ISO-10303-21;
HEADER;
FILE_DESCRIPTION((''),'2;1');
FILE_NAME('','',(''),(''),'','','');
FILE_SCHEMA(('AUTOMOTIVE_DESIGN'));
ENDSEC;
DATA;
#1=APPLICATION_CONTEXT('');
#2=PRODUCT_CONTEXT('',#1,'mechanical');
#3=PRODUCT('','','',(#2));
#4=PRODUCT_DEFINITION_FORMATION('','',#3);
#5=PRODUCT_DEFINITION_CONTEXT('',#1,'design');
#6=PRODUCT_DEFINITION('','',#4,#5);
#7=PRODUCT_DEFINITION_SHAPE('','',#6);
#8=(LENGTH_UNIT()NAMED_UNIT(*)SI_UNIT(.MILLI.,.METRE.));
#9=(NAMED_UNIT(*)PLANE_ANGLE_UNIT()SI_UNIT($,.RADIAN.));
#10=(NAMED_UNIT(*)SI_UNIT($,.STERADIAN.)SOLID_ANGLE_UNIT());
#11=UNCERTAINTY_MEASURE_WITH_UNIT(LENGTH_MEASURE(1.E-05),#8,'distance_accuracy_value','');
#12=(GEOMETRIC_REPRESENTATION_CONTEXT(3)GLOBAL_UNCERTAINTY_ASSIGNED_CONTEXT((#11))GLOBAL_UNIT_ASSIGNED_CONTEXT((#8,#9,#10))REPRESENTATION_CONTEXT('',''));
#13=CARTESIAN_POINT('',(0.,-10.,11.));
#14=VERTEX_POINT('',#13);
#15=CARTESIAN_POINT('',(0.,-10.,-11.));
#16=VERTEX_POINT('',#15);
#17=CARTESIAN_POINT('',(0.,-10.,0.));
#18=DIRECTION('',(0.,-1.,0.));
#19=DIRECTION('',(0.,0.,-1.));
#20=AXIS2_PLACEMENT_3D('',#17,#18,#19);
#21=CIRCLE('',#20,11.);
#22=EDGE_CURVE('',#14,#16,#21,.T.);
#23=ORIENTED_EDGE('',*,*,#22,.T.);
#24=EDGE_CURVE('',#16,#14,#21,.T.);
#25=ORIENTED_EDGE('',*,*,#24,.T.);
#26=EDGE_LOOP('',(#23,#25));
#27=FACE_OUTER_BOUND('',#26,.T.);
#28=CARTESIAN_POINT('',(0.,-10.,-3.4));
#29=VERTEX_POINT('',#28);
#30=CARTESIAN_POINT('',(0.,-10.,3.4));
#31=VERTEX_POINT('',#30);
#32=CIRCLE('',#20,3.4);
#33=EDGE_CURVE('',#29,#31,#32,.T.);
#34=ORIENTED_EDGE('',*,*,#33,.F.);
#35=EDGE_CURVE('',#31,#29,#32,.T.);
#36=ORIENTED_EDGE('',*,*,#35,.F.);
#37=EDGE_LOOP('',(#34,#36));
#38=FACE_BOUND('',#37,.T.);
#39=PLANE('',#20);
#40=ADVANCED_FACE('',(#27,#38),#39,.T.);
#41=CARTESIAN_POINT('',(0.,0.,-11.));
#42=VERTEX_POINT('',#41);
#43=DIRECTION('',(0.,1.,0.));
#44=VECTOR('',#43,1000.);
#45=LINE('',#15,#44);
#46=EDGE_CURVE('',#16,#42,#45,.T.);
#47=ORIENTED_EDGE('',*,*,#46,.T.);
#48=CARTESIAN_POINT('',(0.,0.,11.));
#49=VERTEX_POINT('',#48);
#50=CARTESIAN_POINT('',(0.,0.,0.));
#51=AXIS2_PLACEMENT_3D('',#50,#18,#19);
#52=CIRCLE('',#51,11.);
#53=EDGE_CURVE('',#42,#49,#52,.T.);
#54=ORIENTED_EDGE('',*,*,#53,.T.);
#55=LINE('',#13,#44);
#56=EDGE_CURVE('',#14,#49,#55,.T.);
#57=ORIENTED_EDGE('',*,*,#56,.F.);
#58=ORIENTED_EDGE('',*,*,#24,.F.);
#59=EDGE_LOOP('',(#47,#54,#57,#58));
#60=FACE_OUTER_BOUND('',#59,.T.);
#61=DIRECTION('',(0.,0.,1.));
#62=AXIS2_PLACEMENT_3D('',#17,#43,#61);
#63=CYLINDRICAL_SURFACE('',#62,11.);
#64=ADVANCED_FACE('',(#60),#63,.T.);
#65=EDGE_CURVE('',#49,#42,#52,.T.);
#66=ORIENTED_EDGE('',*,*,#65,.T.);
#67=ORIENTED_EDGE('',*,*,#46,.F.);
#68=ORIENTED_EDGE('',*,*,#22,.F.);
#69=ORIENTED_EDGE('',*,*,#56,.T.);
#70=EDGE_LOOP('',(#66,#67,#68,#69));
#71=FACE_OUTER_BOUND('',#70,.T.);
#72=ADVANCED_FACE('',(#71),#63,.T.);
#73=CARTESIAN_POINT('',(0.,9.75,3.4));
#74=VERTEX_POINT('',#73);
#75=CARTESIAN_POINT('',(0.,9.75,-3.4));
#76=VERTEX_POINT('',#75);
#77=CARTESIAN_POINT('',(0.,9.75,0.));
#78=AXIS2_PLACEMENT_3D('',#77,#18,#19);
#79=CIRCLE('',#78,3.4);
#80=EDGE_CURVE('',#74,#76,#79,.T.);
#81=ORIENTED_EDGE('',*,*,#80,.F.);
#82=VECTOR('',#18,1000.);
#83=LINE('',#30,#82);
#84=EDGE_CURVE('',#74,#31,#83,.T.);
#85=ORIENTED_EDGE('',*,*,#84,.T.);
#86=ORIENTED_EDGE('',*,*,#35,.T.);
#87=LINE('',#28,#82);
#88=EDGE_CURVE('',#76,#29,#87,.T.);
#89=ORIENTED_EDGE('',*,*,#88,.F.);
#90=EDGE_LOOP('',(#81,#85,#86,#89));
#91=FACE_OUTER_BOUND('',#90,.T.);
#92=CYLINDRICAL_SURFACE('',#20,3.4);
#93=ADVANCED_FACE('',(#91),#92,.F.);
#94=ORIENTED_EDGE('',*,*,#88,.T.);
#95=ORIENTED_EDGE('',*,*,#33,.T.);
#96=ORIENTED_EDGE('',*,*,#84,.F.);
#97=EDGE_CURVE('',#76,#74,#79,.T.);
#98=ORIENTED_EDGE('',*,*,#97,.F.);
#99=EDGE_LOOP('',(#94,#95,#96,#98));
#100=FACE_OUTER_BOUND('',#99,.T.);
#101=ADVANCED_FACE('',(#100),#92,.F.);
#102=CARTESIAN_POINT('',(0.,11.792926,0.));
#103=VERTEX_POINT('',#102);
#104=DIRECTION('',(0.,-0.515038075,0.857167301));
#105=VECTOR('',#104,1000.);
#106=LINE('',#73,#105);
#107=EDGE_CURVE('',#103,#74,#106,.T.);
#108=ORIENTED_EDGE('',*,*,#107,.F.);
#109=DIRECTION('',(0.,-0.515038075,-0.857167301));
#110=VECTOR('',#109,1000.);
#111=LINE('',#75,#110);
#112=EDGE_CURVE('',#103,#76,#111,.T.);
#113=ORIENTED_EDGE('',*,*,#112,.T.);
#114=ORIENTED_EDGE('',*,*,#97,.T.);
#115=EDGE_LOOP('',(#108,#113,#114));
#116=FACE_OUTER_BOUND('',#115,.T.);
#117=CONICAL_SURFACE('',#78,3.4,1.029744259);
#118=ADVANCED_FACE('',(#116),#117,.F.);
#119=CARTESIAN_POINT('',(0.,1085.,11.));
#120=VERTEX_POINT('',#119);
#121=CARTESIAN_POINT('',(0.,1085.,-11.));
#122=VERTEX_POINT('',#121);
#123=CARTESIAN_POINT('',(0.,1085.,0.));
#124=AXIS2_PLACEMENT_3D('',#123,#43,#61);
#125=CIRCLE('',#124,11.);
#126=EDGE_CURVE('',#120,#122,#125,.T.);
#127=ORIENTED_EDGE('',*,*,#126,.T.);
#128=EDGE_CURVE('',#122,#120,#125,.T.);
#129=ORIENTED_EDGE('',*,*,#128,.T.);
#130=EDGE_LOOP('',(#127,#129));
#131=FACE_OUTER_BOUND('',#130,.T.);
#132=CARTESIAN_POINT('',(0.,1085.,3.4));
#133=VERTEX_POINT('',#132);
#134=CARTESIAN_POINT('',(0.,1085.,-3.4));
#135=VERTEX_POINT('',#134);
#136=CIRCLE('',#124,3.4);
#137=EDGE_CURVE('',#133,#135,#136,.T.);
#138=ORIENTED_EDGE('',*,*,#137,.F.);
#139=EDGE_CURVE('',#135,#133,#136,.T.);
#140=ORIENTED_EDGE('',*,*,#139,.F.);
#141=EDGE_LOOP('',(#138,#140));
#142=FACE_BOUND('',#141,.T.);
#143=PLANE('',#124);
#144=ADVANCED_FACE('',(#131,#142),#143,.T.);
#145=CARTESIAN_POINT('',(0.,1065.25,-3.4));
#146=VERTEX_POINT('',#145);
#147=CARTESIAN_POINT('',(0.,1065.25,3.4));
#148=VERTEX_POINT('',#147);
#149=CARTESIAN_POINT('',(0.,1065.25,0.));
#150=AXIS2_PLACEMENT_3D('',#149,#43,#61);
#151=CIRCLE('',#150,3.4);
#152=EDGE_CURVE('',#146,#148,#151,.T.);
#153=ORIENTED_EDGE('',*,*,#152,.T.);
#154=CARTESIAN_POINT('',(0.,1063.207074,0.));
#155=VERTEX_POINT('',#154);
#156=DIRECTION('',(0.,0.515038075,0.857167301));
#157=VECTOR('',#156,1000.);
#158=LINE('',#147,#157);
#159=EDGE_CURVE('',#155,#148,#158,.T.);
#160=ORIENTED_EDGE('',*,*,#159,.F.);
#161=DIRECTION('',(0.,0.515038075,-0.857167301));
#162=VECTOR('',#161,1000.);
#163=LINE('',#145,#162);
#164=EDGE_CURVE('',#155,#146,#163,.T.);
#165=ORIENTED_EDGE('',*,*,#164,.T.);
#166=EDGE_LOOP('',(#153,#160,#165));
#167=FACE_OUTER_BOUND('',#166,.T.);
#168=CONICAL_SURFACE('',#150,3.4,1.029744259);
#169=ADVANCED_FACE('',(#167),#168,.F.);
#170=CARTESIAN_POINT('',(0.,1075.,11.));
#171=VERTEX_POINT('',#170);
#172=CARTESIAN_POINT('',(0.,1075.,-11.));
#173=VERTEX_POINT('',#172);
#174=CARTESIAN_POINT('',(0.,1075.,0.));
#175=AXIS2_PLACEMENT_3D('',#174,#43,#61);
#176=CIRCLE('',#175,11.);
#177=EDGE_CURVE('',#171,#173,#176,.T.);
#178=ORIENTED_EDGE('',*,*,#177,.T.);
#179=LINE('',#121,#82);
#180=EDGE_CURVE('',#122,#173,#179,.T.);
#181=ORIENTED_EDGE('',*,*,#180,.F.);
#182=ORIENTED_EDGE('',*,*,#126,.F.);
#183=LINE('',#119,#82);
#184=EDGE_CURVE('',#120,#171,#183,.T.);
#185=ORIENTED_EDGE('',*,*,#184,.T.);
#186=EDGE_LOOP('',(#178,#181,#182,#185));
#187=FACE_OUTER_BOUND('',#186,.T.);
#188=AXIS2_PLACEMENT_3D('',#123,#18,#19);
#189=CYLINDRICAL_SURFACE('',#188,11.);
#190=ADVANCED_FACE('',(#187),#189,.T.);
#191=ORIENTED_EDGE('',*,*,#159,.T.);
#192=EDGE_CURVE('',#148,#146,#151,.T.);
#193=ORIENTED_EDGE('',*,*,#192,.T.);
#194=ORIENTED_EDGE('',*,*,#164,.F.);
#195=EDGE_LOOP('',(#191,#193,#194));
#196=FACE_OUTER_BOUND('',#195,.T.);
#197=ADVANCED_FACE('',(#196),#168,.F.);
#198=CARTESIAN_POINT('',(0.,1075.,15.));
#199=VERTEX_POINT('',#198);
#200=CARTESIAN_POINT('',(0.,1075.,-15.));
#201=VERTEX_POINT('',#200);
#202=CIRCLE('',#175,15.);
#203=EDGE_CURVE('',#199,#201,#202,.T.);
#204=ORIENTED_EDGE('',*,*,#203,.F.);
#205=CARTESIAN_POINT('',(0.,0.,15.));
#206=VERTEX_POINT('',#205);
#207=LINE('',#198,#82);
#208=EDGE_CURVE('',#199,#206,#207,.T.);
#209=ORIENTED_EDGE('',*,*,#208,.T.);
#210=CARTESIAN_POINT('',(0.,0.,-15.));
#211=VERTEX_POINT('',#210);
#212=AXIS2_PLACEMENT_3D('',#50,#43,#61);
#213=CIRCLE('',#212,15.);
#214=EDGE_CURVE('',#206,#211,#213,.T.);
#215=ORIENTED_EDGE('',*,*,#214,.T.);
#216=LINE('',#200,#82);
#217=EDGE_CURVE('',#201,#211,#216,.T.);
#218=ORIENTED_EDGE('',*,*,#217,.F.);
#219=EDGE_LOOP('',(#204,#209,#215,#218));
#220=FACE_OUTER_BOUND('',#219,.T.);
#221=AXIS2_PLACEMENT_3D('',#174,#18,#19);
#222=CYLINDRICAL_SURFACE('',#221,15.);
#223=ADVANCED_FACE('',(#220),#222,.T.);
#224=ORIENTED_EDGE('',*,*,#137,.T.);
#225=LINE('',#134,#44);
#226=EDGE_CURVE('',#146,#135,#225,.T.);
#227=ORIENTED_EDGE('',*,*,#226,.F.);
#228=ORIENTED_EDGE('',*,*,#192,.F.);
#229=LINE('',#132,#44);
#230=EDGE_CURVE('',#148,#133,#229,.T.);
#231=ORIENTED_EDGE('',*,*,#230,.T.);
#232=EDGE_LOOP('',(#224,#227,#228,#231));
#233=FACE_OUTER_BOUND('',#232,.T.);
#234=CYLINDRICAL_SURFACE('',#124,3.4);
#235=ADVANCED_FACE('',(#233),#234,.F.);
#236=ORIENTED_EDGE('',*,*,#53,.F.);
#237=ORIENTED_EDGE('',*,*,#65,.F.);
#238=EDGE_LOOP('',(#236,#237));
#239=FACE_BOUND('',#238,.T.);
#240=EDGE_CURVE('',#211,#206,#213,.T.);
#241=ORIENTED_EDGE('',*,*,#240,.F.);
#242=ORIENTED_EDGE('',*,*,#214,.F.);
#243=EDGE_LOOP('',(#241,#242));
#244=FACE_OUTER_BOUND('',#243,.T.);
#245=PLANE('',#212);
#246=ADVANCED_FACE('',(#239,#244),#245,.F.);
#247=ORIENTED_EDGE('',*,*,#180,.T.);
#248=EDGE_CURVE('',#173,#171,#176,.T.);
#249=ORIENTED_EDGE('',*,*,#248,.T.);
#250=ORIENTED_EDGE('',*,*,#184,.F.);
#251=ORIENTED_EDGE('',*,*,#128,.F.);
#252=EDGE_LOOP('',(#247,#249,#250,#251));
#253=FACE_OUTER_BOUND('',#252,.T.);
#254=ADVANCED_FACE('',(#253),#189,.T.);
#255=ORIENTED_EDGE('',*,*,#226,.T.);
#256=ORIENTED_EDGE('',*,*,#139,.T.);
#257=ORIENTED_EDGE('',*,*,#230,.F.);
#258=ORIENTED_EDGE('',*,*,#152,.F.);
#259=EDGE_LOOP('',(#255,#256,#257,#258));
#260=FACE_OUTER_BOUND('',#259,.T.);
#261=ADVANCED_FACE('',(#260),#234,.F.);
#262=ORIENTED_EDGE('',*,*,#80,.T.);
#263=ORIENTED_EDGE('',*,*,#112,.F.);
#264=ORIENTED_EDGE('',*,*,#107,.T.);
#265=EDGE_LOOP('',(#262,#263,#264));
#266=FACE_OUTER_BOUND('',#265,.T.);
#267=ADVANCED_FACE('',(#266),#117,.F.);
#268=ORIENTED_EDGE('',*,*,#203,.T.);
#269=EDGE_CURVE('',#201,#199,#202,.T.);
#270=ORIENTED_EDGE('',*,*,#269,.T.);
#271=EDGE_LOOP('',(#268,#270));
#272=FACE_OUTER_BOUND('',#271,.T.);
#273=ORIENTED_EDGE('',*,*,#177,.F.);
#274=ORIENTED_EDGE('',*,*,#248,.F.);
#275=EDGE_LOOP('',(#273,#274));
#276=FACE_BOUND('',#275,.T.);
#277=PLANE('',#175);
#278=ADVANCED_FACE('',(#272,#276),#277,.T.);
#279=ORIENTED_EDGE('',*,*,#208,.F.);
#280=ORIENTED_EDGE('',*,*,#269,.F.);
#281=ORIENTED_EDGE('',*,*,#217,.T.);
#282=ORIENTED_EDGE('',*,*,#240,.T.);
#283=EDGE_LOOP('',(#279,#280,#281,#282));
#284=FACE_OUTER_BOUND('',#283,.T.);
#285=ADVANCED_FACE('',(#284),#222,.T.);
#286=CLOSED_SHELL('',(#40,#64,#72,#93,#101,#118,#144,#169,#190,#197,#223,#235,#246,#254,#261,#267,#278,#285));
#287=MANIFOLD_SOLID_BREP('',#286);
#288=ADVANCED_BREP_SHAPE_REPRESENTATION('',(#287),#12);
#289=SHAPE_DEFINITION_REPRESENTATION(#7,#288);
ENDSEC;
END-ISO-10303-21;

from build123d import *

# Parameters (mm, degrees)
SKETCH1_R             = 15
BOSS_EXTRUDE1_DEPTH   = 1075
SKETCH2_R             = 11
BOSS_EXTRUDE2_DEPTH   = 10
BOSS_EXTRUDE3_START   = 10
SKETCH3_R             = 11
BOSS_EXTRUDE3_DEPTH   = 10
M8_TAPPED_HOLE1_D     = 6.8
M8_TAPPED_HOLE1_DEPTH = 19.75
M8_TAPPED_HOLE1_TIP   = 2.042926105
M8_TAPPED_HOLE2_D     = 6.8
M8_TAPPED_HOLE2_DEPTH = 19.75
M8_TAPPED_HOLE2_TIP   = 2.042926105


with BuildPart() as part:
    # Sketch1 → Boss-Extrude1 (new body)
    with BuildSketch(Plane(origin=(0, 0, 0), x_dir=(1, 0, 0), z_dir=(0, 1, 0))):
        with Locations(Location((0, 0, 0), (0, 0, 270))):
            Circle(SKETCH1_R)
    extrude(amount=BOSS_EXTRUDE1_DEPTH)

    # Sketch2 → Boss-Extrude2 (add)
    with BuildSketch(Plane(origin=(0, 1075, 0), x_dir=(1, 0, 0), z_dir=(0, 1, 0))):
        with Locations(Location((0, 0, 0), (0, 0, 270))):
            Circle(SKETCH2_R)
    extrude(amount=BOSS_EXTRUDE2_DEPTH)

    # Sketch3 → Boss-Extrude3 (add)
    with BuildSketch(Plane.XZ.offset(BOSS_EXTRUDE3_START)):
        with Locations(Location((0, 0, 0), (0, 0, 90))):
            Circle(SKETCH3_R)
    extrude(amount=-BOSS_EXTRUDE3_DEPTH)

    # M8 Tapped Hole1
    with Locations(Plane(origin=(0, -10, 0), x_dir=(-1, 0, 0), z_dir=(0, -1, 0))):
        with Locations((0, 0)):
            Hole(M8_TAPPED_HOLE1_D / 2, depth=M8_TAPPED_HOLE1_DEPTH)
            with Locations((0, 0, -(M8_TAPPED_HOLE1_DEPTH + M8_TAPPED_HOLE1_TIP / 2))):  # 118° drill point
                Cone(0, M8_TAPPED_HOLE1_D / 2, M8_TAPPED_HOLE1_TIP, mode=Mode.SUBTRACT)

    # M8 Tapped Hole2
    with Locations(Plane(origin=(0, 1085, 0), x_dir=(1, 0, 0), z_dir=(0, 1, 0))):
        with Locations((0, 0)):
            Hole(M8_TAPPED_HOLE2_D / 2, depth=M8_TAPPED_HOLE2_DEPTH)
            with Locations((0, 0, -(M8_TAPPED_HOLE2_DEPTH + M8_TAPPED_HOLE2_TIP / 2))):  # 118° drill point
                Cone(0, M8_TAPPED_HOLE2_D / 2, M8_TAPPED_HOLE2_TIP, mode=Mode.SUBTRACT)


solid = part.part
